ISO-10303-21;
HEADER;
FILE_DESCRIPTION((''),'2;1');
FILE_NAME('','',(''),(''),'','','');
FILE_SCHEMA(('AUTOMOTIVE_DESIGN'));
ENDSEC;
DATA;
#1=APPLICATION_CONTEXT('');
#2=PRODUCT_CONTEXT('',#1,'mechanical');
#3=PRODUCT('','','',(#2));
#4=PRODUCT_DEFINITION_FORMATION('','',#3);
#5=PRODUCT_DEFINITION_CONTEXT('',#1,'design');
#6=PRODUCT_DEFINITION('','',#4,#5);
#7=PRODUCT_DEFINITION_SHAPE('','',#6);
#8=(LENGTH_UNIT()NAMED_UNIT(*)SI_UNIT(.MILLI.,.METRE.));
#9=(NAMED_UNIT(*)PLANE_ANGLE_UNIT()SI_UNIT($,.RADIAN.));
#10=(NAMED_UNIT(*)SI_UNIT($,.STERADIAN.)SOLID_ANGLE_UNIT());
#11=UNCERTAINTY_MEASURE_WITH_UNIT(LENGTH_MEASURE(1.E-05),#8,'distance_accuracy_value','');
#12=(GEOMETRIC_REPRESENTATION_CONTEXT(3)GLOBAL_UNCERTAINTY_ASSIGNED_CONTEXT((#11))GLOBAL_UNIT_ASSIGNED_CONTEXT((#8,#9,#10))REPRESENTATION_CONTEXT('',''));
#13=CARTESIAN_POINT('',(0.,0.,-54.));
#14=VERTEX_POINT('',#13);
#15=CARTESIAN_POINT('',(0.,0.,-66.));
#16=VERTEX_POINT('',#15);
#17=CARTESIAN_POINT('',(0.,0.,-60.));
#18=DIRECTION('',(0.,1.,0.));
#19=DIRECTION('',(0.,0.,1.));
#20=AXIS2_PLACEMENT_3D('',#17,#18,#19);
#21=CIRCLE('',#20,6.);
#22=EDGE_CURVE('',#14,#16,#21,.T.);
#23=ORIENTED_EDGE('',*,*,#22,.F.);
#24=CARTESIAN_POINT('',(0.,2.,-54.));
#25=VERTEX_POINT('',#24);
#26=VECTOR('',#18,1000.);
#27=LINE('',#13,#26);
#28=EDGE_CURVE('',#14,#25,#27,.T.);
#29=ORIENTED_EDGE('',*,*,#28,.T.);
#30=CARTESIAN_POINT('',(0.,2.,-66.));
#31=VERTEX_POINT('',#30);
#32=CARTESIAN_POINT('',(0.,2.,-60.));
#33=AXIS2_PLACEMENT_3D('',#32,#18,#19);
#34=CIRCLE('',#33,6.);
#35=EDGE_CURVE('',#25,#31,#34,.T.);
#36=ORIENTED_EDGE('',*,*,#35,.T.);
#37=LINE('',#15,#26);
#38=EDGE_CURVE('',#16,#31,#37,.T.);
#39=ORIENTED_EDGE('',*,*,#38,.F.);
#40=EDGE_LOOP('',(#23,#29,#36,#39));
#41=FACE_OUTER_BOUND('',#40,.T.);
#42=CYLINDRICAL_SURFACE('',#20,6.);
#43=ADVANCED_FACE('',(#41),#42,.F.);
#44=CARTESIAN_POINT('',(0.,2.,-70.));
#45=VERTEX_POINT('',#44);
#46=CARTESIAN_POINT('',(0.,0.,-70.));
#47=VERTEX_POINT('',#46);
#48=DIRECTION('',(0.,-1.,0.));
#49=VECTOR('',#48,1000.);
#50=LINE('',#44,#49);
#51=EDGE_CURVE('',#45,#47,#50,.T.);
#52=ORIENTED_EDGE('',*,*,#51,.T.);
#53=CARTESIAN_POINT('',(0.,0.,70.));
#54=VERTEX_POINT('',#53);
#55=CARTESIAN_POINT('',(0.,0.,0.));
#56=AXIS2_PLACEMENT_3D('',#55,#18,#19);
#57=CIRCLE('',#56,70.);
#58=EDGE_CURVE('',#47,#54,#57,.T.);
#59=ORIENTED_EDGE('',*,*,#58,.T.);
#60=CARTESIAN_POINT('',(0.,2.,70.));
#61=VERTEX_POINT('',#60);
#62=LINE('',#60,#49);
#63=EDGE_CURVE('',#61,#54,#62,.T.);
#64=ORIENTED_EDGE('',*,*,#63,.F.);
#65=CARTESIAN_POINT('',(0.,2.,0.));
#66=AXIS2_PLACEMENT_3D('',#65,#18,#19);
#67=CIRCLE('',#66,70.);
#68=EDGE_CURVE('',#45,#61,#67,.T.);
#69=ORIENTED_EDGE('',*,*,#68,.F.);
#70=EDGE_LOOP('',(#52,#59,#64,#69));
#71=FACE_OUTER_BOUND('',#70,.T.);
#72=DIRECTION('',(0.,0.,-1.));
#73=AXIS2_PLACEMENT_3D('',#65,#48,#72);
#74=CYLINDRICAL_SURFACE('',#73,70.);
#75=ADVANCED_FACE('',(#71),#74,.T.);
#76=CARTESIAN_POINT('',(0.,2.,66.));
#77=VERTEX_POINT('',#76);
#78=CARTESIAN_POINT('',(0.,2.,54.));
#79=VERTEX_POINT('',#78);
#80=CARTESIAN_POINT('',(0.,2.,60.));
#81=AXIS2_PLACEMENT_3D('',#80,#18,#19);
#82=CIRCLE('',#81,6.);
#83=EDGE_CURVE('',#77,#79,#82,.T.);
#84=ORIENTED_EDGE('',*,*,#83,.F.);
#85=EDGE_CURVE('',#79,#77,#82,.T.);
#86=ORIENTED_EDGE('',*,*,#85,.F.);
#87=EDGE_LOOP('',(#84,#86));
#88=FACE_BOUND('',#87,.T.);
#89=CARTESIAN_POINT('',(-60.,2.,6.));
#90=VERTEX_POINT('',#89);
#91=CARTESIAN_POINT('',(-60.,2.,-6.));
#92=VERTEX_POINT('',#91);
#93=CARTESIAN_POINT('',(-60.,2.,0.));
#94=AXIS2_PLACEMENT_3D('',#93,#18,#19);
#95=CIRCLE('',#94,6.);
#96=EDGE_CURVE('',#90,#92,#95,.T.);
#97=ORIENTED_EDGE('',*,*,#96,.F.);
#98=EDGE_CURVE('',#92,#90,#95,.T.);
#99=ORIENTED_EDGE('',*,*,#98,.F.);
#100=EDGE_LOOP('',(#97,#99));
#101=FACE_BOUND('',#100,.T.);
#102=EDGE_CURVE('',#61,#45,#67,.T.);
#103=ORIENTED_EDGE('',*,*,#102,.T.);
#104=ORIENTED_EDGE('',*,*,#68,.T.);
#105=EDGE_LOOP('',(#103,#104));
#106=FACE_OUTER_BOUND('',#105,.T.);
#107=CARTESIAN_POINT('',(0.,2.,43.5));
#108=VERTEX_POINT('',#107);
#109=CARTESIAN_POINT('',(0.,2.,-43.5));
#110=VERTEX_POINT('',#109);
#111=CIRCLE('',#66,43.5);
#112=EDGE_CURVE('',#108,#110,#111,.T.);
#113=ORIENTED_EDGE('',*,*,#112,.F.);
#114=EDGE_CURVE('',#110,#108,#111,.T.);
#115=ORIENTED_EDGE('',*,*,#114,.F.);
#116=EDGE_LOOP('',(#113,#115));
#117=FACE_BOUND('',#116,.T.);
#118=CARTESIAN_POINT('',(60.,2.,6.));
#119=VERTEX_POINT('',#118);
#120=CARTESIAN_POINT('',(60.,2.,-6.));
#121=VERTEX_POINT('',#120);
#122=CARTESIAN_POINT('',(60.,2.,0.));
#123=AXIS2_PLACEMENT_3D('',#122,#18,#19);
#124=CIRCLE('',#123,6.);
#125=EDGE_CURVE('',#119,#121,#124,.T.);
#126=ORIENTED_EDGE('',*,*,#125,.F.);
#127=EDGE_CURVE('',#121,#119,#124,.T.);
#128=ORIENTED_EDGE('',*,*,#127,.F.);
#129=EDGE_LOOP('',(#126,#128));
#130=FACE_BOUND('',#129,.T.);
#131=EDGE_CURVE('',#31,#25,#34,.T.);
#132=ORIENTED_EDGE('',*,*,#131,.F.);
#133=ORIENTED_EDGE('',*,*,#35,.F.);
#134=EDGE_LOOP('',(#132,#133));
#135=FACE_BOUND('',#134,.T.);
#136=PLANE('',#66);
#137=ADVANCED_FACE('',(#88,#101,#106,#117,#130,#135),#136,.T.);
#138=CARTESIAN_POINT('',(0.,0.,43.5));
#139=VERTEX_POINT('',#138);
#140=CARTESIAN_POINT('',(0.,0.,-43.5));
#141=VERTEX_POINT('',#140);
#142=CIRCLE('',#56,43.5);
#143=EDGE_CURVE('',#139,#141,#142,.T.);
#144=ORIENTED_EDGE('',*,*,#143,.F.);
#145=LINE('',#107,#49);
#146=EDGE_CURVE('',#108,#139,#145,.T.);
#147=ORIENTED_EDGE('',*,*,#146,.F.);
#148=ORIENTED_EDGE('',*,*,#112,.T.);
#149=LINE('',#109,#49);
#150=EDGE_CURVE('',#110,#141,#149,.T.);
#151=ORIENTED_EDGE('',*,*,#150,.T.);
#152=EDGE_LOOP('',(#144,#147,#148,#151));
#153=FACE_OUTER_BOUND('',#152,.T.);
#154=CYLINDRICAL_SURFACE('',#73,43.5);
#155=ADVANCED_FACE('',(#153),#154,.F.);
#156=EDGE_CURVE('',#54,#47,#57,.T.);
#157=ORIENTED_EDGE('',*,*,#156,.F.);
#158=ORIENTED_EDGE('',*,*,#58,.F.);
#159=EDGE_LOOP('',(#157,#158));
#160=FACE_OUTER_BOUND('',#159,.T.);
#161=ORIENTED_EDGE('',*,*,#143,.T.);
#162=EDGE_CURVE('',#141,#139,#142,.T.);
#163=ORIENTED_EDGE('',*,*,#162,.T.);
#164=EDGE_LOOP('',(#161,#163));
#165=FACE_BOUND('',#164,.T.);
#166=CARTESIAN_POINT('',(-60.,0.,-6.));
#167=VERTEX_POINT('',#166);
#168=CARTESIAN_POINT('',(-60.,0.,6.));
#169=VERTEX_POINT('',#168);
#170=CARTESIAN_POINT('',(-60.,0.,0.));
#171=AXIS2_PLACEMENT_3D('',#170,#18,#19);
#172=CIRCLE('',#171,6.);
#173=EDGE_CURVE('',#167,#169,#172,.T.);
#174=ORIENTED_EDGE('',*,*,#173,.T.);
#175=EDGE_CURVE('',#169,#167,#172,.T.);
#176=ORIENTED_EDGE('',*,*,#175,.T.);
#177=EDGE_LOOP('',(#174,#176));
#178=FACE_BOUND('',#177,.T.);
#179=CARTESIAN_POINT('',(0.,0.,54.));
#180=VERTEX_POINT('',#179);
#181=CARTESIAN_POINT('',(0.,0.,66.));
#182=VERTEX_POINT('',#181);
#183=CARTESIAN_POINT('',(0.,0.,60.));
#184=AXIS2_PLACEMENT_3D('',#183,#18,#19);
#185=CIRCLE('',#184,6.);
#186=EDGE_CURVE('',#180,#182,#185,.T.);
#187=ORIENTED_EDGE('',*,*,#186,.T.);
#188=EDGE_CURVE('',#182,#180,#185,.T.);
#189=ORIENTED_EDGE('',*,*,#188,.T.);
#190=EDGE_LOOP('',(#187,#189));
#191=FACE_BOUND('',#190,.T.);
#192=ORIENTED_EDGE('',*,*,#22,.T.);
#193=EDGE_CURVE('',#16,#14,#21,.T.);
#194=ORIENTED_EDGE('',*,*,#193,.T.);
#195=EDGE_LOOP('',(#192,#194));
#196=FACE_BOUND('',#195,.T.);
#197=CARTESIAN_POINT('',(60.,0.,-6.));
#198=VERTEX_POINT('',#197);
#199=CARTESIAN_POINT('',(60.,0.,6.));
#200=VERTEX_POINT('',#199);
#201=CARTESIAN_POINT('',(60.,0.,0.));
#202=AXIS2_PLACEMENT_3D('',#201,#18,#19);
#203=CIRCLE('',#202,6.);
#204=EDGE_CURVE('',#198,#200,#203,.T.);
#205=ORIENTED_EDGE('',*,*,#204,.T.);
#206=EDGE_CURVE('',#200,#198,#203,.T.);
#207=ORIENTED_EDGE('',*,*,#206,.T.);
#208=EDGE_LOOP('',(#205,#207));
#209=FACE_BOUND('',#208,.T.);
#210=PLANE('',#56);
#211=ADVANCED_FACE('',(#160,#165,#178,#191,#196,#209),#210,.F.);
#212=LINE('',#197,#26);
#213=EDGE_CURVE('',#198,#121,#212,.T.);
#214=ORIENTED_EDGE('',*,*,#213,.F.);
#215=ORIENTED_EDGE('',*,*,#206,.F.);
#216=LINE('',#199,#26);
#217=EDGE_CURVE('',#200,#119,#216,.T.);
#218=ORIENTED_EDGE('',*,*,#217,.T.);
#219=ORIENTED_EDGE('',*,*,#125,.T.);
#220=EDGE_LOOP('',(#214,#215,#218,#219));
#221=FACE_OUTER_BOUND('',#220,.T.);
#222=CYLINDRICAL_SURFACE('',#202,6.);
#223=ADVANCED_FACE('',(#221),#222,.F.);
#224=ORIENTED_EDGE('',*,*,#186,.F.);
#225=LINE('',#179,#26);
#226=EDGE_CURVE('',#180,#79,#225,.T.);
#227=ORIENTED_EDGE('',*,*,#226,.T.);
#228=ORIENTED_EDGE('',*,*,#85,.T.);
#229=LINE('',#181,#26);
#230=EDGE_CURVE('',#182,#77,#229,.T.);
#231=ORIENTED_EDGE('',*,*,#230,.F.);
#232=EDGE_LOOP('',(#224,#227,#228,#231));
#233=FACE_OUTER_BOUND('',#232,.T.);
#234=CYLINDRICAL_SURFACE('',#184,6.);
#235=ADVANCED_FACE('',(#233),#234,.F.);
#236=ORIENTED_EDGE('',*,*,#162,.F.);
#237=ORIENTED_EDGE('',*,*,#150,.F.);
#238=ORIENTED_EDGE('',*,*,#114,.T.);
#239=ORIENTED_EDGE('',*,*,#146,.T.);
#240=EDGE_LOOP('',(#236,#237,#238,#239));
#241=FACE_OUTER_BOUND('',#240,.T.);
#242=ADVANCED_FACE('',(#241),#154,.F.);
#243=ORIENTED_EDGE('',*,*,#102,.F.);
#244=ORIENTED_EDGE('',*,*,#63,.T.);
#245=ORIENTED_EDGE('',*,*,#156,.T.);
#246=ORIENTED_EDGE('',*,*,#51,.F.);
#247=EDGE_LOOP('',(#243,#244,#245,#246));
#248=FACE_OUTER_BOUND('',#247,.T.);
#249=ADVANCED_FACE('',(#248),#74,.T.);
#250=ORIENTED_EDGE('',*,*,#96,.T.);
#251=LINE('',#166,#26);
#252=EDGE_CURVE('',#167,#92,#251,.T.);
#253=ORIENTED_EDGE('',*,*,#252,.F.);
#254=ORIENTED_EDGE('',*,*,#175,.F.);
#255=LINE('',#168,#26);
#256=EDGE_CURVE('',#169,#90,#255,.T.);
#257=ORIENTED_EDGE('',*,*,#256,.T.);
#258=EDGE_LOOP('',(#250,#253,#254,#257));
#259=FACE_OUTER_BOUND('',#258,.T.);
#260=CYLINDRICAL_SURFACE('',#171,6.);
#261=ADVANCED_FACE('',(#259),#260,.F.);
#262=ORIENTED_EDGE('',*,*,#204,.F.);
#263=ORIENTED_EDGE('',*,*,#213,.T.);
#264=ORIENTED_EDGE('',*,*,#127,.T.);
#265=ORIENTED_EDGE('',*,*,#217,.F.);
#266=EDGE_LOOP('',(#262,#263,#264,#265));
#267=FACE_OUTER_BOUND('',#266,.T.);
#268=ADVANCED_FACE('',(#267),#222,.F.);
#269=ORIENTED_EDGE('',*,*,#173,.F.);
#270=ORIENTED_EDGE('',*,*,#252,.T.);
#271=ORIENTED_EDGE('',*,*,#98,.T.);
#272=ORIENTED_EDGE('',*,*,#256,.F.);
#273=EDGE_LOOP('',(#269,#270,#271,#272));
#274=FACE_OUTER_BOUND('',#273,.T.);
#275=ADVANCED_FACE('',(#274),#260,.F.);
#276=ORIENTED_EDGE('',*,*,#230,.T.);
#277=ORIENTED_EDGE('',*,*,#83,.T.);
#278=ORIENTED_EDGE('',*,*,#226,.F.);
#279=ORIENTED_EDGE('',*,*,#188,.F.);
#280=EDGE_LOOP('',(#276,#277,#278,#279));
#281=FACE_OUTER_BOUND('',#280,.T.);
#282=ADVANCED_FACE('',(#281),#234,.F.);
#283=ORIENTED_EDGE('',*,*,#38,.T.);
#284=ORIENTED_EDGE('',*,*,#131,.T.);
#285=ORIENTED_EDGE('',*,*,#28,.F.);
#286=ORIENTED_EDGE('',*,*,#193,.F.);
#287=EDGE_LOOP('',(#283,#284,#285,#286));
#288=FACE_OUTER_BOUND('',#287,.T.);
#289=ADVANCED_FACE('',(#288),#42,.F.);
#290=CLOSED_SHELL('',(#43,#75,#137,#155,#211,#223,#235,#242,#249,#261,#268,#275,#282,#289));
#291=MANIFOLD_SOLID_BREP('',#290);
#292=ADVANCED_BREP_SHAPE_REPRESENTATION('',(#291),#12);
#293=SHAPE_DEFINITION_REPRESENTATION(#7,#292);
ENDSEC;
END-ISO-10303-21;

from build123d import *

# Parameters (mm, degrees)
SKETCH_1_R          = 70
SKETCH_1_R_2        = 43.5
EXTRUDE_1_DEPTH     = 2
SKETCH_3_R          = 6
CUT_EXTRUDE_1_DEPTH = 100.015150356


with BuildPart() as part:
    # 草图1 → 凸台-拉伸1 (new body)
    with BuildSketch(Plane(origin=(0, 0, 0), x_dir=(1, 0, 0), z_dir=(0, 1, 0))):
        with Locations(Location((0, 0, 0), (0, 0, 270))):
            Circle(SKETCH_1_R)
        with Locations(Location((0, 0, 0), (0, 0, 270))):
            Circle(SKETCH_1_R_2, mode=Mode.SUBTRACT)
    extrude(amount=EXTRUDE_1_DEPTH)

    # 草图3 → 切除-拉伸1 (cut, through all)
    with BuildSketch(Plane(origin=(0, 2, 0), x_dir=(1, 0, 0), z_dir=(0, 1, 0))):
        with Locations(Location((0, 60, 0), (0, 0, 270))):
            Circle(SKETCH_3_R)
        with Locations(Location((60, 0, 0), (0, 0, 270))):
            Circle(SKETCH_3_R)
        with Locations(Location((0, -60, 0), (0, 0, 270))):
            Circle(SKETCH_3_R)
        with Locations(Location((-60, 0, 0), (0, 0, 270))):
            Circle(SKETCH_3_R)
    extrude(amount=-CUT_EXTRUDE_1_DEPTH, mode=Mode.SUBTRACT)


solid = part.part
